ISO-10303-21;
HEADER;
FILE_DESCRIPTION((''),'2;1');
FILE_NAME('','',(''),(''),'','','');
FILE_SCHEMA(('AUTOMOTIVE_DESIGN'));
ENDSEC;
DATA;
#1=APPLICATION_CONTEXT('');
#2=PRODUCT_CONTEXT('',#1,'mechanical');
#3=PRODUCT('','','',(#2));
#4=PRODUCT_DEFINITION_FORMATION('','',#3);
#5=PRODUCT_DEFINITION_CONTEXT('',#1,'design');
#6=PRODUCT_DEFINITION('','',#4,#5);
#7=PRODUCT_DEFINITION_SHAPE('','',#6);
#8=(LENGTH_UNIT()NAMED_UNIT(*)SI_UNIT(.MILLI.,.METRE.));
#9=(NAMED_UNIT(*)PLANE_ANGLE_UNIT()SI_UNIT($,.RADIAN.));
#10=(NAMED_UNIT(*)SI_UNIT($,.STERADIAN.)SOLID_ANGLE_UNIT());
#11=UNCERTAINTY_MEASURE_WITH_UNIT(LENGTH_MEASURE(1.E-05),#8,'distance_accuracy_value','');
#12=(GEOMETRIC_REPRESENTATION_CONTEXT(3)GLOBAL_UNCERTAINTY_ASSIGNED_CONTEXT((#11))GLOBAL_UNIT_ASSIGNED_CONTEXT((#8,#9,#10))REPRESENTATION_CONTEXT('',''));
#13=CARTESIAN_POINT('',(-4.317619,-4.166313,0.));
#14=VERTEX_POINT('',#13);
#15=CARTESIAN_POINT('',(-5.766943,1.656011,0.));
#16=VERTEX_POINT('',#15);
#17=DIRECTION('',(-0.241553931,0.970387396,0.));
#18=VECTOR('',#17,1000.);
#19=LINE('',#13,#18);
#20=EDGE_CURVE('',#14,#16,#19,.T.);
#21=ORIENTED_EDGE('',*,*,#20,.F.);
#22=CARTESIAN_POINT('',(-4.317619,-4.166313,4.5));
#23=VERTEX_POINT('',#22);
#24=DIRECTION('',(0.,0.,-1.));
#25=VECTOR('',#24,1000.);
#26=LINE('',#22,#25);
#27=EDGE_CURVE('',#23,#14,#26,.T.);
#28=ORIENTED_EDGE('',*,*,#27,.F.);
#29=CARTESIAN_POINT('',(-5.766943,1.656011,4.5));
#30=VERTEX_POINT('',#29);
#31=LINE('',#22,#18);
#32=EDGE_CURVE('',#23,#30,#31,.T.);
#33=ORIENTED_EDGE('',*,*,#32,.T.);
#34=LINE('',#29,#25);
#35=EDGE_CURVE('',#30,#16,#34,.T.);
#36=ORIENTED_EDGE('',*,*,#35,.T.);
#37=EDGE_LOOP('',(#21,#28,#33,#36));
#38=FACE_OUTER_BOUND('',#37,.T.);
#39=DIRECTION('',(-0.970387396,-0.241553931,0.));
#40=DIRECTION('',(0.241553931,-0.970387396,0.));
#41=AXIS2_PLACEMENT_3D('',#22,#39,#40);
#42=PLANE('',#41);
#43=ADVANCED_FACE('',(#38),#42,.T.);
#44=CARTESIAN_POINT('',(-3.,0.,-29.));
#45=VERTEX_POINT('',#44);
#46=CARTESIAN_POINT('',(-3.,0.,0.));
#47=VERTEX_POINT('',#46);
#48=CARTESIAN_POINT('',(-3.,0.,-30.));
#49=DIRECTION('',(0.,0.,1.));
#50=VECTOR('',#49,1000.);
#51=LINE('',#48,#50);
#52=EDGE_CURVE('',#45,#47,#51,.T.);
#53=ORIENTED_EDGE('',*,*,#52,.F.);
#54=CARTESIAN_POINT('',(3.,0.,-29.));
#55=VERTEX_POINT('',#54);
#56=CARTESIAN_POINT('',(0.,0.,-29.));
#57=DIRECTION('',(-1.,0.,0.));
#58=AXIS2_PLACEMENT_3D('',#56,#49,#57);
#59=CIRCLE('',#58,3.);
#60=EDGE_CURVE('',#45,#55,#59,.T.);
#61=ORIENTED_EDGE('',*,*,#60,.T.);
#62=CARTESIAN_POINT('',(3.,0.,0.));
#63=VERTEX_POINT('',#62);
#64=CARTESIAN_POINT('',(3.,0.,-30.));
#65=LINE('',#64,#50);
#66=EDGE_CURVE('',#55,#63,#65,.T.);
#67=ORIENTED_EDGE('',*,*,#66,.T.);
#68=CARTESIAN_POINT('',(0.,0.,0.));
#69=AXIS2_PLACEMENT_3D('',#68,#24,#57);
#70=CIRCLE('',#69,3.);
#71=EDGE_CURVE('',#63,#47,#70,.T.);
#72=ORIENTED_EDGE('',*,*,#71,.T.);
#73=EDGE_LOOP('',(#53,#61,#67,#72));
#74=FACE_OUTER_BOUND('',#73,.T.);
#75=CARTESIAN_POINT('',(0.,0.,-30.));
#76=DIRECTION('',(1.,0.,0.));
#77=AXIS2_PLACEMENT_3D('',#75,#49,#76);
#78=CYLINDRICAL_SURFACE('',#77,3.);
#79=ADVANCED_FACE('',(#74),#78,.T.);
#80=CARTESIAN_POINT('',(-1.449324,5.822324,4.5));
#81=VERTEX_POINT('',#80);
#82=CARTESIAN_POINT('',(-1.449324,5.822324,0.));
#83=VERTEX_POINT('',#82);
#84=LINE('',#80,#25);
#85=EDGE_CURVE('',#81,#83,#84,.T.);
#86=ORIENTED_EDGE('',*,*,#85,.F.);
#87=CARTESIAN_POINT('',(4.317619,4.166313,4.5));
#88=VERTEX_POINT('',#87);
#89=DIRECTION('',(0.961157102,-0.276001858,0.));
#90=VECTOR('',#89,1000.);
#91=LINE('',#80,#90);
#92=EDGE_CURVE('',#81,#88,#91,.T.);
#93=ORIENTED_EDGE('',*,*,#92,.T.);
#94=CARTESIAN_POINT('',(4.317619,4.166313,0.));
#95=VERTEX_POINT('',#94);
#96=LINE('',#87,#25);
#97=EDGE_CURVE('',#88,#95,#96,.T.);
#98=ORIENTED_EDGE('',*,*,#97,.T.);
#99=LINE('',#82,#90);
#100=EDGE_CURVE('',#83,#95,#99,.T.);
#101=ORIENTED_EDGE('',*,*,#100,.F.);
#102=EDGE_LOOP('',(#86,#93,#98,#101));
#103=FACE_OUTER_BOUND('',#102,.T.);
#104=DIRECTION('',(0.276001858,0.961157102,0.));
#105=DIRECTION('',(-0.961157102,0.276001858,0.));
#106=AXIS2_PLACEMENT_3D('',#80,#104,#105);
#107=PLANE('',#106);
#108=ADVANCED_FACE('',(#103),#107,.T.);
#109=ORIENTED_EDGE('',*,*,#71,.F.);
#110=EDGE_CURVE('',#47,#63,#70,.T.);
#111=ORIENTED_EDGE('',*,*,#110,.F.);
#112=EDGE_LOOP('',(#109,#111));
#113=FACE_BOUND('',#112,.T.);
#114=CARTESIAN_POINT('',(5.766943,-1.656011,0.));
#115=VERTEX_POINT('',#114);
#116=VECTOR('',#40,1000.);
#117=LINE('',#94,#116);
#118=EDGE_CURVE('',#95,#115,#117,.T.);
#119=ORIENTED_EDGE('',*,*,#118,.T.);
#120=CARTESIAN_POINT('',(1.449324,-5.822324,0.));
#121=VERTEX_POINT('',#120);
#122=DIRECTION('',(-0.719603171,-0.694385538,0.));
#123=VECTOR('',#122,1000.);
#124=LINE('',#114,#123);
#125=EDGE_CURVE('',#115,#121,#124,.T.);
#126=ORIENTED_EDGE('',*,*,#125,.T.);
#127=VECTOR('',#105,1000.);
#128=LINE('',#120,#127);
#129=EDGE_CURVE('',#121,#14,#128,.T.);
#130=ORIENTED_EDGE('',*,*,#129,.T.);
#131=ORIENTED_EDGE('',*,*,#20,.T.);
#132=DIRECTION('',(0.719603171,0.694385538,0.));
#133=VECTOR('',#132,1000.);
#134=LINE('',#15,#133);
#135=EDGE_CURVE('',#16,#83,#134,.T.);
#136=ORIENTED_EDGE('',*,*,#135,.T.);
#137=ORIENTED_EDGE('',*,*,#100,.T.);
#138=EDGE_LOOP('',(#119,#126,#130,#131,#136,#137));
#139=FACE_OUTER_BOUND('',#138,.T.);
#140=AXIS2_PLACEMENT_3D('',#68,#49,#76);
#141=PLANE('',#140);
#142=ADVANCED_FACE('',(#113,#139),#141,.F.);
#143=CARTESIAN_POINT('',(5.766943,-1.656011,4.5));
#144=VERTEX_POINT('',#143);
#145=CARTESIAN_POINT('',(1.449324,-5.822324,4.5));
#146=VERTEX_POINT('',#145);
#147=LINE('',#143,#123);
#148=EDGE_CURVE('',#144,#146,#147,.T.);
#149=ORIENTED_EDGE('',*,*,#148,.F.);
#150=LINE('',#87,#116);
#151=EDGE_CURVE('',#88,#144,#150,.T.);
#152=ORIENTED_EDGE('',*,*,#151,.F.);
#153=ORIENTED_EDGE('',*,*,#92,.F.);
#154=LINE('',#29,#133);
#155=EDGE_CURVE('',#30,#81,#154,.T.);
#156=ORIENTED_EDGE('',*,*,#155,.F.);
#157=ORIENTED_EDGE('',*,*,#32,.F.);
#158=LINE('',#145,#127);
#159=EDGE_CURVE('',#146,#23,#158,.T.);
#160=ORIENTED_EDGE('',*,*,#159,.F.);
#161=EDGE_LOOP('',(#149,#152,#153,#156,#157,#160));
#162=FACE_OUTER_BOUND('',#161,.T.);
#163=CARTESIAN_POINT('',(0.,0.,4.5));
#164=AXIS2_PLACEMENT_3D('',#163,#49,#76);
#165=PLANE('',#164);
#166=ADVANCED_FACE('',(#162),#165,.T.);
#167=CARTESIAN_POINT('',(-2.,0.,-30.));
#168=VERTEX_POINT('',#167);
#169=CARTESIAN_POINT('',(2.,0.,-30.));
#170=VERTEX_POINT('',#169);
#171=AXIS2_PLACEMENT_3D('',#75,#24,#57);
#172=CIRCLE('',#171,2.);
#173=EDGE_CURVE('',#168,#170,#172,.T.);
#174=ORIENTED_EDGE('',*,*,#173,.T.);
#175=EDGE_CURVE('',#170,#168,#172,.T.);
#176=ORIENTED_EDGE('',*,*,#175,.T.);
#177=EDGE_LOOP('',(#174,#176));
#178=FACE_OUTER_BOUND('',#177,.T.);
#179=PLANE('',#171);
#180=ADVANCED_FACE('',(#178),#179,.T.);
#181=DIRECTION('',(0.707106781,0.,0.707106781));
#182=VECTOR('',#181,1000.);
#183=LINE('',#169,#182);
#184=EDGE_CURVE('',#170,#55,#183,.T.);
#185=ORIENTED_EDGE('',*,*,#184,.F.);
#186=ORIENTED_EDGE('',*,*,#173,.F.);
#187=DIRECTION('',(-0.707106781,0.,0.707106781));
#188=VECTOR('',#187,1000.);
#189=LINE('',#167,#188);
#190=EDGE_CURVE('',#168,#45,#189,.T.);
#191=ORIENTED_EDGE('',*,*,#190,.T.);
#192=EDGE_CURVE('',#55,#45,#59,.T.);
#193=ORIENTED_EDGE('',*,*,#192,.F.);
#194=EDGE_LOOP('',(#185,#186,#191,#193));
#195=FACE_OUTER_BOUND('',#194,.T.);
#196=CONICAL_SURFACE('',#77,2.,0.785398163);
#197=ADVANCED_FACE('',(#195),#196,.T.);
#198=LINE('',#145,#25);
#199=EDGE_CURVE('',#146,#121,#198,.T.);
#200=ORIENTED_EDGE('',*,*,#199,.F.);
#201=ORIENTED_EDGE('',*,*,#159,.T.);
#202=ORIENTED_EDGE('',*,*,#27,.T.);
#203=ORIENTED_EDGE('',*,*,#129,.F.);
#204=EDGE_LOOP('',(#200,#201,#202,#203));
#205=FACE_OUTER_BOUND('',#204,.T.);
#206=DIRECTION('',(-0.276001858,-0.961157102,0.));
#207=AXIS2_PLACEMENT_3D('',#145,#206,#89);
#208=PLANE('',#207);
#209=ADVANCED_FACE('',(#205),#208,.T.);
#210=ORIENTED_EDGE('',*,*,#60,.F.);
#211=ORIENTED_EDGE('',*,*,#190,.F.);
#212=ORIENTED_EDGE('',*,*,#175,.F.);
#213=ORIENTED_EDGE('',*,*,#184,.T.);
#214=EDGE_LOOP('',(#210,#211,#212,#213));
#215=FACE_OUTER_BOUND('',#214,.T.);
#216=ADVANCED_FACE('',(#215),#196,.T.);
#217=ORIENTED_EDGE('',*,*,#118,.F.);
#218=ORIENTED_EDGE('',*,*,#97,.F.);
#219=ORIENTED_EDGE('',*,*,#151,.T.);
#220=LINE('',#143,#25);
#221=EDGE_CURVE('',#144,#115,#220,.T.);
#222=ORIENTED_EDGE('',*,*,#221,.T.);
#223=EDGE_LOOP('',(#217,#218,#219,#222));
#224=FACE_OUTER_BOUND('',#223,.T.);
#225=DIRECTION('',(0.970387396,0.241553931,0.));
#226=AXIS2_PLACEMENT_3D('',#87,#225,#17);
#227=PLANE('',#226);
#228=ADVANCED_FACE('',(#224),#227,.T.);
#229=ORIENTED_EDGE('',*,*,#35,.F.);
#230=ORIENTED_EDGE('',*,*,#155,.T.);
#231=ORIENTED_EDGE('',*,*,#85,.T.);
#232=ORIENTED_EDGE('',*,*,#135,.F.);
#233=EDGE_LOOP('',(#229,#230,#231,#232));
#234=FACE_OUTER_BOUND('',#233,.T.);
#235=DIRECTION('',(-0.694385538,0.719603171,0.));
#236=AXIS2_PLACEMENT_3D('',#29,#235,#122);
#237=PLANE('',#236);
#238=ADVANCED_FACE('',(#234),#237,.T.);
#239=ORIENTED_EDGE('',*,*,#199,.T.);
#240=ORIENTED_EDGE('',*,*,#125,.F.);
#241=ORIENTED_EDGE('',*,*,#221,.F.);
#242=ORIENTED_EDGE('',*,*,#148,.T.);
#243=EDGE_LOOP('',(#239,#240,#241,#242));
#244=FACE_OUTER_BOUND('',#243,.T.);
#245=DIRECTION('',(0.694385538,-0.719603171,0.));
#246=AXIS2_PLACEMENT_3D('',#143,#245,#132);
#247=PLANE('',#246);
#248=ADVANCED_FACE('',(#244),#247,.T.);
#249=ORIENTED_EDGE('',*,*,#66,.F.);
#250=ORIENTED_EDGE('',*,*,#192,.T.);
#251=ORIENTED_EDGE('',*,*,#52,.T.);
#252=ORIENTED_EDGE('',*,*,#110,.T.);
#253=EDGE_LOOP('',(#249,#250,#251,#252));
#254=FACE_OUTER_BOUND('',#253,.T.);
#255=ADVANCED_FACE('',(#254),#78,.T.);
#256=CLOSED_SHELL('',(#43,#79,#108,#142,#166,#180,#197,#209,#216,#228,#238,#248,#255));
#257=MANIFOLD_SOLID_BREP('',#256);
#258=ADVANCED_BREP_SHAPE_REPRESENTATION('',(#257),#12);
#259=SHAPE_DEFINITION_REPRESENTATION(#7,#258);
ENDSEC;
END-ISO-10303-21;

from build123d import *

# Parameters (mm, degrees)
SKETCH1_R           = 6
BOSS_EXTRUDE1_DEPTH = 4.5
SKETCH2_OUTSIDE_W   = 17.512
SKETCH2_OUTSIDE_H   = 17.512
CUT_EXTRUDE1_DEPTH  = 4.5
SKETCH3_R           = 3
BOSS_EXTRUDE2_DEPTH = 30
CHAMFER1_SIZE       = 1


with BuildPart() as part:
    # Sketch1 → Boss-Extrude1 (new body)
    with BuildSketch(Plane.XY):
        Circle(SKETCH1_R)
    extrude(amount=BOSS_EXTRUDE1_DEPTH)

    # Sketch2 outside → Cut-Extrude1 (cut)
    with BuildSketch(Plane(origin=(0, 0, 0), x_dir=(-1, 0, 0), z_dir=(0, 0, -1))):
        Rectangle(SKETCH2_OUTSIDE_W, SKETCH2_OUTSIDE_H)
        Polygon((4.317619028, -4.16631323), (5.766942611, 1.656011147), (1.449323583, 5.822324377), (-4.317619028, 4.16631323), (-5.766942611, -1.656011147), (-1.449323583, -5.822324377), align=None, mode=Mode.SUBTRACT)
    extrude(amount=-CUT_EXTRUDE1_DEPTH, mode=Mode.SUBTRACT)

    # Sketch3 → Boss-Extrude2 (add)
    with BuildSketch(Plane(origin=(0, 0, 0), x_dir=(-1, 0, 0), z_dir=(0, 0, -1))):
        Circle(SKETCH3_R)
    extrude(amount=BOSS_EXTRUDE2_DEPTH)

    # Chamfer1
    chamfer1_edges = [part.edges().sort_by_distance(p)[0] for p in [
        (3, 0, -30),
    ]]
    chamfer(chamfer1_edges, length=CHAMFER1_SIZE)


solid = part.part
